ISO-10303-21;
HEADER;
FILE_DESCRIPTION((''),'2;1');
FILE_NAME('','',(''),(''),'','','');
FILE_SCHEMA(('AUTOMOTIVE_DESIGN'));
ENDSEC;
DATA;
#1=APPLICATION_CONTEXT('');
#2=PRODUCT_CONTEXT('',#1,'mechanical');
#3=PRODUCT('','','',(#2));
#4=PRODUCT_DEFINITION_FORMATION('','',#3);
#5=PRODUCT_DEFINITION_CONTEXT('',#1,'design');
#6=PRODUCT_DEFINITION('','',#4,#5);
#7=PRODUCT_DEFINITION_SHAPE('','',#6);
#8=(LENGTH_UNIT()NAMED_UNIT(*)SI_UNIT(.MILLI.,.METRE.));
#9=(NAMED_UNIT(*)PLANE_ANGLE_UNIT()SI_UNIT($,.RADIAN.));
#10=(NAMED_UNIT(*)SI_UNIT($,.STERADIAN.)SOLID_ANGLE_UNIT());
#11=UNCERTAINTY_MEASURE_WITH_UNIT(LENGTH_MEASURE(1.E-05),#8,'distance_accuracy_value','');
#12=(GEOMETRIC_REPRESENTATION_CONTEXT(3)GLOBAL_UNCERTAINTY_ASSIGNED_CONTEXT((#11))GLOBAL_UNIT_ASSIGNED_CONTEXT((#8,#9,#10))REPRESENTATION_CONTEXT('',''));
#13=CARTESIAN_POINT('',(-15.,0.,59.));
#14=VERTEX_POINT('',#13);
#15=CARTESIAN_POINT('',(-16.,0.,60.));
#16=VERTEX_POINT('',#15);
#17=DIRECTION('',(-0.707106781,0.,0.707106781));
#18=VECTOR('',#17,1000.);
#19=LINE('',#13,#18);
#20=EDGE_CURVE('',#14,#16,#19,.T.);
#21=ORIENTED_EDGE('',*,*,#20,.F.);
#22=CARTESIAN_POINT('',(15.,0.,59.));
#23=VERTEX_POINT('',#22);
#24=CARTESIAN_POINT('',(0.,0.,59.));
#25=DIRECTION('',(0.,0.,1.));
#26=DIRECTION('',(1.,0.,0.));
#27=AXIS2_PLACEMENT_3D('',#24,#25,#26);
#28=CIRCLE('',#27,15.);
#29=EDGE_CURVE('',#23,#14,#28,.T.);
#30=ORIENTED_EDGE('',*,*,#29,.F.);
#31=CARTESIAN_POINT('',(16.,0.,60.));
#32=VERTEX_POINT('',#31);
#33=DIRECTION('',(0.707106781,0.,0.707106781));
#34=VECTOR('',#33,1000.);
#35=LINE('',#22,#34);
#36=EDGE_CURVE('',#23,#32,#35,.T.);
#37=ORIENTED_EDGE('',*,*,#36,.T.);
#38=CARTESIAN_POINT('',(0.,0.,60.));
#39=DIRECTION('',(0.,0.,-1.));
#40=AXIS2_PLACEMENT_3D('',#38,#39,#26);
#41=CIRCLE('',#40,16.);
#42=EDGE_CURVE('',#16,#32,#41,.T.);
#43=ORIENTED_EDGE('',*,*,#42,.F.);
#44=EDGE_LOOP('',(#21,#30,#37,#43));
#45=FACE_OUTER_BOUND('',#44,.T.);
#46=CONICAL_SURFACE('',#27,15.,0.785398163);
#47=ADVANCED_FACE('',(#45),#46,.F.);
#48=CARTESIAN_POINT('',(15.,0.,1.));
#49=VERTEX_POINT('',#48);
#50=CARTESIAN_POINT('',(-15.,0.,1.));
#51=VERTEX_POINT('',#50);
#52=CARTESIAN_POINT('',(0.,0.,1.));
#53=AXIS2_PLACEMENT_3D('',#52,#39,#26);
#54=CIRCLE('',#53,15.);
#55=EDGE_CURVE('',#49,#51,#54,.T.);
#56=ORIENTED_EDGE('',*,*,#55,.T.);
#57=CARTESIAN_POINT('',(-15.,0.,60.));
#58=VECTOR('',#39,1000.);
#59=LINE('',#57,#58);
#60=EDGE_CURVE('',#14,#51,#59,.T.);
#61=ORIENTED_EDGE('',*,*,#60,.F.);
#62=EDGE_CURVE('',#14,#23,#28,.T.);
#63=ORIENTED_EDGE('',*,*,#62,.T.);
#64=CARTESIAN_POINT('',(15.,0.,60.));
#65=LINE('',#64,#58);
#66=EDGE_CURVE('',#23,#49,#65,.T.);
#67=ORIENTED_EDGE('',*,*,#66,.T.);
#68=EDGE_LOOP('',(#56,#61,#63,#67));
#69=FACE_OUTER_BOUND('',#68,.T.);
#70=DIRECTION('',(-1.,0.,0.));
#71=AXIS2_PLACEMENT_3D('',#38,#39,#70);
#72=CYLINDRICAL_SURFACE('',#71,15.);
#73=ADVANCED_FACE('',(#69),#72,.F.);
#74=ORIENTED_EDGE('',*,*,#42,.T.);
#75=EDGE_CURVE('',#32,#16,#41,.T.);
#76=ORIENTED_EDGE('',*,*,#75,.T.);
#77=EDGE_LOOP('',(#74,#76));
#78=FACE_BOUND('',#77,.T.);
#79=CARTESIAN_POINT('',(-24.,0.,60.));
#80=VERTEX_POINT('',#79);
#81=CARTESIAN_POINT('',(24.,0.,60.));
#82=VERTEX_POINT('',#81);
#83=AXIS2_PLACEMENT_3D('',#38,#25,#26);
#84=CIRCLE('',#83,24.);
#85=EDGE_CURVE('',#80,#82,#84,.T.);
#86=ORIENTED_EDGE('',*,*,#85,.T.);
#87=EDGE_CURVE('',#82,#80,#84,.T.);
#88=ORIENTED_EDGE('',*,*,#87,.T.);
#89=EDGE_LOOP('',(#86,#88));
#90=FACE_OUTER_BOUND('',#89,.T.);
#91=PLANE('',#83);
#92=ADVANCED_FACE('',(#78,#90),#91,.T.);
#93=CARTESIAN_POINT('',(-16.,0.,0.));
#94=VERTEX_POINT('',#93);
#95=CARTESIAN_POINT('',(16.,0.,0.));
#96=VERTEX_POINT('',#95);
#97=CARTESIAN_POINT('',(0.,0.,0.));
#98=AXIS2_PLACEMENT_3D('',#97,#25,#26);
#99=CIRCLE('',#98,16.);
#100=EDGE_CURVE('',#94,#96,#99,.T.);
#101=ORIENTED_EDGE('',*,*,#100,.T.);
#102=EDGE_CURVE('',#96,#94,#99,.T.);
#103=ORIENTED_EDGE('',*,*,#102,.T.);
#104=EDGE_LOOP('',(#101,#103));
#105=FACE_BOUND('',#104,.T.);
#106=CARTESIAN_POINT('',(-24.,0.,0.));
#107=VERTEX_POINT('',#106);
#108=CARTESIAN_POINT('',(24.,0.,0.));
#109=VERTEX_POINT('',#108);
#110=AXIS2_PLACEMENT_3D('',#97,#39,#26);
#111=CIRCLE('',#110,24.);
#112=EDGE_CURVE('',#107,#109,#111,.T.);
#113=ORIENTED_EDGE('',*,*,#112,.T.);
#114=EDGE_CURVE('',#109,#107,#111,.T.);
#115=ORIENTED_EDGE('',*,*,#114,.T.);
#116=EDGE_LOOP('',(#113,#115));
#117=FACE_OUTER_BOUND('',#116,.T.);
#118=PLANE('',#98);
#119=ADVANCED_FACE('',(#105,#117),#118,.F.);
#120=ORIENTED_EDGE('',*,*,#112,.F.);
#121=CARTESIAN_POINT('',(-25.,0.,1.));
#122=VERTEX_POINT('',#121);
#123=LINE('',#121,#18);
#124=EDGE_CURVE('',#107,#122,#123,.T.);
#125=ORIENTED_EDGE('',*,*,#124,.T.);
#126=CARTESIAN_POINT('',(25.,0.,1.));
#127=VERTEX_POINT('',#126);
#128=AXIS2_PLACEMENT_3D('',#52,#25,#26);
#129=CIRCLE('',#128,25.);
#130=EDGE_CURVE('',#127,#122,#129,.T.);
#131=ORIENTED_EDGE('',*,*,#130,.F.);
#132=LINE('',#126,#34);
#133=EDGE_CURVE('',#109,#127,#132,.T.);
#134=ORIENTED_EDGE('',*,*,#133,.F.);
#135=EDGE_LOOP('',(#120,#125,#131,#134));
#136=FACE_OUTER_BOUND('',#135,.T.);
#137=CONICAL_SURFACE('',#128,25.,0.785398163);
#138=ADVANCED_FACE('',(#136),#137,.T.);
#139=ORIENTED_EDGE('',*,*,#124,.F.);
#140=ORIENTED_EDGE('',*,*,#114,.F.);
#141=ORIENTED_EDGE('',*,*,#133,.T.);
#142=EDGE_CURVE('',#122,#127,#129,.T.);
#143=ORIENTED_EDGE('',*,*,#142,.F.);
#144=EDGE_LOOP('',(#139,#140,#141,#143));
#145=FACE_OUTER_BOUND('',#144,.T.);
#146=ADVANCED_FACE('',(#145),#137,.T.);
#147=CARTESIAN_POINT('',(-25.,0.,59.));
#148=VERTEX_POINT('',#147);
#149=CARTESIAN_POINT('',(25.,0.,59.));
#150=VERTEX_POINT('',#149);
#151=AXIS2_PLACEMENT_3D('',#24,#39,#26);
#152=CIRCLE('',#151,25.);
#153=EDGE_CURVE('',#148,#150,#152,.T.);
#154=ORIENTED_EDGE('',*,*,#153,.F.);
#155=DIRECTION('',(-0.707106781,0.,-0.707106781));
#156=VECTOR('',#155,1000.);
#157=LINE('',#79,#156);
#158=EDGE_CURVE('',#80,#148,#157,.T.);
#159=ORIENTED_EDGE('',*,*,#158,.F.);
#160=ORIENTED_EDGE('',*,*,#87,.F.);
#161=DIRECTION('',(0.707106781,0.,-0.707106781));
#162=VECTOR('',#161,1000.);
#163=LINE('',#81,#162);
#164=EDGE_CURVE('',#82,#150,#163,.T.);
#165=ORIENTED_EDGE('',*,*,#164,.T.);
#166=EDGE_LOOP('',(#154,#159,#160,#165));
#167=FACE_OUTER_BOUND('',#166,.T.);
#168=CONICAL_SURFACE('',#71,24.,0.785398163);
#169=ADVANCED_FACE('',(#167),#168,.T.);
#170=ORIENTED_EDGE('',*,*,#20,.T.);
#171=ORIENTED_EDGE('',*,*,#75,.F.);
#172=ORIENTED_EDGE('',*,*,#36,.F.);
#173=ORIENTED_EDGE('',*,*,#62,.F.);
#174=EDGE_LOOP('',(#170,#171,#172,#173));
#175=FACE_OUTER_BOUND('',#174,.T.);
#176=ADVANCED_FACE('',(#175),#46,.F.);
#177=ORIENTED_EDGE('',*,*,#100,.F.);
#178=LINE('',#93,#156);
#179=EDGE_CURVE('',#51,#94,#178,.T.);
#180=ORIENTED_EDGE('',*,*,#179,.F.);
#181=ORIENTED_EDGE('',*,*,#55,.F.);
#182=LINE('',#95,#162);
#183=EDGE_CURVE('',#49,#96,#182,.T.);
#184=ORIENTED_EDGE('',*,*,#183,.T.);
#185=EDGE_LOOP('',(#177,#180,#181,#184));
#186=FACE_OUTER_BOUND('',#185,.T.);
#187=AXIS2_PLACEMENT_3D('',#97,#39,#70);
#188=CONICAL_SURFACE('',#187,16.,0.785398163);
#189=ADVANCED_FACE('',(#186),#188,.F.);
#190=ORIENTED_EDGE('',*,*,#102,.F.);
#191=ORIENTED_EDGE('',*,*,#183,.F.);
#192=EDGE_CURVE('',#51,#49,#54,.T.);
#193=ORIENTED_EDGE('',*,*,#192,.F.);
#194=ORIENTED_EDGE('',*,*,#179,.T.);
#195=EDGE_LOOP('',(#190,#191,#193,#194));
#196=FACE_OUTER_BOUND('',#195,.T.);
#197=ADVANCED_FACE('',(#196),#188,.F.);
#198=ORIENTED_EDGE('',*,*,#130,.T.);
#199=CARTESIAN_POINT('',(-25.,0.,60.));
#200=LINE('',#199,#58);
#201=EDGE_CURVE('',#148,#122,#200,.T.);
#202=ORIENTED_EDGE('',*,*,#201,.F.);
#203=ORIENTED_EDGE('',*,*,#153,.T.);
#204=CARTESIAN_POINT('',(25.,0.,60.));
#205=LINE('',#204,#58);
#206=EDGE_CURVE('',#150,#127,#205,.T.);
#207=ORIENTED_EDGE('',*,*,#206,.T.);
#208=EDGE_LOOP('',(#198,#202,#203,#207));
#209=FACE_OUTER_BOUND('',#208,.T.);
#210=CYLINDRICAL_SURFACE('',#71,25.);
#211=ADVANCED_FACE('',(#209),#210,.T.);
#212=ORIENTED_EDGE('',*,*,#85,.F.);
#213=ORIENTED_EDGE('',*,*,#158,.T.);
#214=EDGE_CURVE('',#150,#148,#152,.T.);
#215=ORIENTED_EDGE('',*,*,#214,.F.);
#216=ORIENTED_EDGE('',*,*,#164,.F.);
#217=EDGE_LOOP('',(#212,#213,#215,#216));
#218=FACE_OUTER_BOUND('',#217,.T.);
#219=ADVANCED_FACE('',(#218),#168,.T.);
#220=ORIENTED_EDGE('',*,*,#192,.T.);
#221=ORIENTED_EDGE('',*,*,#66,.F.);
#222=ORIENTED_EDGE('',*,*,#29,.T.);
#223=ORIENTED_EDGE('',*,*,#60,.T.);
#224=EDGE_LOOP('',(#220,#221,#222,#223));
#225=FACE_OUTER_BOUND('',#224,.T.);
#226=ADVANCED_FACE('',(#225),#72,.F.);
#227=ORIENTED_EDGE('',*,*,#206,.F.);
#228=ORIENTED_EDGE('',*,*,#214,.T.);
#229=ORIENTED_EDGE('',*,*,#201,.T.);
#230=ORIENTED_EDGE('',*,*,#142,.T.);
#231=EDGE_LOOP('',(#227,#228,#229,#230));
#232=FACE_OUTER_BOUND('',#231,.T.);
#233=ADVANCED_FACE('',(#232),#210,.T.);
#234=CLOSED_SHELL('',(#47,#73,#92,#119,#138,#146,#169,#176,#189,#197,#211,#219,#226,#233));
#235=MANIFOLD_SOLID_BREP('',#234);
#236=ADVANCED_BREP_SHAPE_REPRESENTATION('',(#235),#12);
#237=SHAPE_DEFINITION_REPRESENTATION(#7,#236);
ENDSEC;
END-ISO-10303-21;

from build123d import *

# Parameters (mm, degrees)
SKETCH1_R           = 25
SKETCH1_R_2         = 15
BOSS_EXTRUDE1_DEPTH = 60
CHAMFER1_SIZE       = 1


with BuildPart() as part:
    # Sketch1 → Boss-Extrude1 (new body)
    with BuildSketch(Plane.XY):
        Circle(SKETCH1_R)
        Circle(SKETCH1_R_2, mode=Mode.SUBTRACT)
    extrude(amount=BOSS_EXTRUDE1_DEPTH)

    # Chamfer1
    chamfer1_edges = [part.edges().sort_by_distance(p)[0] for p in [
        (-25, 0, 0),
        (-25, 0, 60),
        (-15, 0, 0),
        (-15, 0, 60),
    ]]
    chamfer(chamfer1_edges, length=CHAMFER1_SIZE)


solid = part.part
